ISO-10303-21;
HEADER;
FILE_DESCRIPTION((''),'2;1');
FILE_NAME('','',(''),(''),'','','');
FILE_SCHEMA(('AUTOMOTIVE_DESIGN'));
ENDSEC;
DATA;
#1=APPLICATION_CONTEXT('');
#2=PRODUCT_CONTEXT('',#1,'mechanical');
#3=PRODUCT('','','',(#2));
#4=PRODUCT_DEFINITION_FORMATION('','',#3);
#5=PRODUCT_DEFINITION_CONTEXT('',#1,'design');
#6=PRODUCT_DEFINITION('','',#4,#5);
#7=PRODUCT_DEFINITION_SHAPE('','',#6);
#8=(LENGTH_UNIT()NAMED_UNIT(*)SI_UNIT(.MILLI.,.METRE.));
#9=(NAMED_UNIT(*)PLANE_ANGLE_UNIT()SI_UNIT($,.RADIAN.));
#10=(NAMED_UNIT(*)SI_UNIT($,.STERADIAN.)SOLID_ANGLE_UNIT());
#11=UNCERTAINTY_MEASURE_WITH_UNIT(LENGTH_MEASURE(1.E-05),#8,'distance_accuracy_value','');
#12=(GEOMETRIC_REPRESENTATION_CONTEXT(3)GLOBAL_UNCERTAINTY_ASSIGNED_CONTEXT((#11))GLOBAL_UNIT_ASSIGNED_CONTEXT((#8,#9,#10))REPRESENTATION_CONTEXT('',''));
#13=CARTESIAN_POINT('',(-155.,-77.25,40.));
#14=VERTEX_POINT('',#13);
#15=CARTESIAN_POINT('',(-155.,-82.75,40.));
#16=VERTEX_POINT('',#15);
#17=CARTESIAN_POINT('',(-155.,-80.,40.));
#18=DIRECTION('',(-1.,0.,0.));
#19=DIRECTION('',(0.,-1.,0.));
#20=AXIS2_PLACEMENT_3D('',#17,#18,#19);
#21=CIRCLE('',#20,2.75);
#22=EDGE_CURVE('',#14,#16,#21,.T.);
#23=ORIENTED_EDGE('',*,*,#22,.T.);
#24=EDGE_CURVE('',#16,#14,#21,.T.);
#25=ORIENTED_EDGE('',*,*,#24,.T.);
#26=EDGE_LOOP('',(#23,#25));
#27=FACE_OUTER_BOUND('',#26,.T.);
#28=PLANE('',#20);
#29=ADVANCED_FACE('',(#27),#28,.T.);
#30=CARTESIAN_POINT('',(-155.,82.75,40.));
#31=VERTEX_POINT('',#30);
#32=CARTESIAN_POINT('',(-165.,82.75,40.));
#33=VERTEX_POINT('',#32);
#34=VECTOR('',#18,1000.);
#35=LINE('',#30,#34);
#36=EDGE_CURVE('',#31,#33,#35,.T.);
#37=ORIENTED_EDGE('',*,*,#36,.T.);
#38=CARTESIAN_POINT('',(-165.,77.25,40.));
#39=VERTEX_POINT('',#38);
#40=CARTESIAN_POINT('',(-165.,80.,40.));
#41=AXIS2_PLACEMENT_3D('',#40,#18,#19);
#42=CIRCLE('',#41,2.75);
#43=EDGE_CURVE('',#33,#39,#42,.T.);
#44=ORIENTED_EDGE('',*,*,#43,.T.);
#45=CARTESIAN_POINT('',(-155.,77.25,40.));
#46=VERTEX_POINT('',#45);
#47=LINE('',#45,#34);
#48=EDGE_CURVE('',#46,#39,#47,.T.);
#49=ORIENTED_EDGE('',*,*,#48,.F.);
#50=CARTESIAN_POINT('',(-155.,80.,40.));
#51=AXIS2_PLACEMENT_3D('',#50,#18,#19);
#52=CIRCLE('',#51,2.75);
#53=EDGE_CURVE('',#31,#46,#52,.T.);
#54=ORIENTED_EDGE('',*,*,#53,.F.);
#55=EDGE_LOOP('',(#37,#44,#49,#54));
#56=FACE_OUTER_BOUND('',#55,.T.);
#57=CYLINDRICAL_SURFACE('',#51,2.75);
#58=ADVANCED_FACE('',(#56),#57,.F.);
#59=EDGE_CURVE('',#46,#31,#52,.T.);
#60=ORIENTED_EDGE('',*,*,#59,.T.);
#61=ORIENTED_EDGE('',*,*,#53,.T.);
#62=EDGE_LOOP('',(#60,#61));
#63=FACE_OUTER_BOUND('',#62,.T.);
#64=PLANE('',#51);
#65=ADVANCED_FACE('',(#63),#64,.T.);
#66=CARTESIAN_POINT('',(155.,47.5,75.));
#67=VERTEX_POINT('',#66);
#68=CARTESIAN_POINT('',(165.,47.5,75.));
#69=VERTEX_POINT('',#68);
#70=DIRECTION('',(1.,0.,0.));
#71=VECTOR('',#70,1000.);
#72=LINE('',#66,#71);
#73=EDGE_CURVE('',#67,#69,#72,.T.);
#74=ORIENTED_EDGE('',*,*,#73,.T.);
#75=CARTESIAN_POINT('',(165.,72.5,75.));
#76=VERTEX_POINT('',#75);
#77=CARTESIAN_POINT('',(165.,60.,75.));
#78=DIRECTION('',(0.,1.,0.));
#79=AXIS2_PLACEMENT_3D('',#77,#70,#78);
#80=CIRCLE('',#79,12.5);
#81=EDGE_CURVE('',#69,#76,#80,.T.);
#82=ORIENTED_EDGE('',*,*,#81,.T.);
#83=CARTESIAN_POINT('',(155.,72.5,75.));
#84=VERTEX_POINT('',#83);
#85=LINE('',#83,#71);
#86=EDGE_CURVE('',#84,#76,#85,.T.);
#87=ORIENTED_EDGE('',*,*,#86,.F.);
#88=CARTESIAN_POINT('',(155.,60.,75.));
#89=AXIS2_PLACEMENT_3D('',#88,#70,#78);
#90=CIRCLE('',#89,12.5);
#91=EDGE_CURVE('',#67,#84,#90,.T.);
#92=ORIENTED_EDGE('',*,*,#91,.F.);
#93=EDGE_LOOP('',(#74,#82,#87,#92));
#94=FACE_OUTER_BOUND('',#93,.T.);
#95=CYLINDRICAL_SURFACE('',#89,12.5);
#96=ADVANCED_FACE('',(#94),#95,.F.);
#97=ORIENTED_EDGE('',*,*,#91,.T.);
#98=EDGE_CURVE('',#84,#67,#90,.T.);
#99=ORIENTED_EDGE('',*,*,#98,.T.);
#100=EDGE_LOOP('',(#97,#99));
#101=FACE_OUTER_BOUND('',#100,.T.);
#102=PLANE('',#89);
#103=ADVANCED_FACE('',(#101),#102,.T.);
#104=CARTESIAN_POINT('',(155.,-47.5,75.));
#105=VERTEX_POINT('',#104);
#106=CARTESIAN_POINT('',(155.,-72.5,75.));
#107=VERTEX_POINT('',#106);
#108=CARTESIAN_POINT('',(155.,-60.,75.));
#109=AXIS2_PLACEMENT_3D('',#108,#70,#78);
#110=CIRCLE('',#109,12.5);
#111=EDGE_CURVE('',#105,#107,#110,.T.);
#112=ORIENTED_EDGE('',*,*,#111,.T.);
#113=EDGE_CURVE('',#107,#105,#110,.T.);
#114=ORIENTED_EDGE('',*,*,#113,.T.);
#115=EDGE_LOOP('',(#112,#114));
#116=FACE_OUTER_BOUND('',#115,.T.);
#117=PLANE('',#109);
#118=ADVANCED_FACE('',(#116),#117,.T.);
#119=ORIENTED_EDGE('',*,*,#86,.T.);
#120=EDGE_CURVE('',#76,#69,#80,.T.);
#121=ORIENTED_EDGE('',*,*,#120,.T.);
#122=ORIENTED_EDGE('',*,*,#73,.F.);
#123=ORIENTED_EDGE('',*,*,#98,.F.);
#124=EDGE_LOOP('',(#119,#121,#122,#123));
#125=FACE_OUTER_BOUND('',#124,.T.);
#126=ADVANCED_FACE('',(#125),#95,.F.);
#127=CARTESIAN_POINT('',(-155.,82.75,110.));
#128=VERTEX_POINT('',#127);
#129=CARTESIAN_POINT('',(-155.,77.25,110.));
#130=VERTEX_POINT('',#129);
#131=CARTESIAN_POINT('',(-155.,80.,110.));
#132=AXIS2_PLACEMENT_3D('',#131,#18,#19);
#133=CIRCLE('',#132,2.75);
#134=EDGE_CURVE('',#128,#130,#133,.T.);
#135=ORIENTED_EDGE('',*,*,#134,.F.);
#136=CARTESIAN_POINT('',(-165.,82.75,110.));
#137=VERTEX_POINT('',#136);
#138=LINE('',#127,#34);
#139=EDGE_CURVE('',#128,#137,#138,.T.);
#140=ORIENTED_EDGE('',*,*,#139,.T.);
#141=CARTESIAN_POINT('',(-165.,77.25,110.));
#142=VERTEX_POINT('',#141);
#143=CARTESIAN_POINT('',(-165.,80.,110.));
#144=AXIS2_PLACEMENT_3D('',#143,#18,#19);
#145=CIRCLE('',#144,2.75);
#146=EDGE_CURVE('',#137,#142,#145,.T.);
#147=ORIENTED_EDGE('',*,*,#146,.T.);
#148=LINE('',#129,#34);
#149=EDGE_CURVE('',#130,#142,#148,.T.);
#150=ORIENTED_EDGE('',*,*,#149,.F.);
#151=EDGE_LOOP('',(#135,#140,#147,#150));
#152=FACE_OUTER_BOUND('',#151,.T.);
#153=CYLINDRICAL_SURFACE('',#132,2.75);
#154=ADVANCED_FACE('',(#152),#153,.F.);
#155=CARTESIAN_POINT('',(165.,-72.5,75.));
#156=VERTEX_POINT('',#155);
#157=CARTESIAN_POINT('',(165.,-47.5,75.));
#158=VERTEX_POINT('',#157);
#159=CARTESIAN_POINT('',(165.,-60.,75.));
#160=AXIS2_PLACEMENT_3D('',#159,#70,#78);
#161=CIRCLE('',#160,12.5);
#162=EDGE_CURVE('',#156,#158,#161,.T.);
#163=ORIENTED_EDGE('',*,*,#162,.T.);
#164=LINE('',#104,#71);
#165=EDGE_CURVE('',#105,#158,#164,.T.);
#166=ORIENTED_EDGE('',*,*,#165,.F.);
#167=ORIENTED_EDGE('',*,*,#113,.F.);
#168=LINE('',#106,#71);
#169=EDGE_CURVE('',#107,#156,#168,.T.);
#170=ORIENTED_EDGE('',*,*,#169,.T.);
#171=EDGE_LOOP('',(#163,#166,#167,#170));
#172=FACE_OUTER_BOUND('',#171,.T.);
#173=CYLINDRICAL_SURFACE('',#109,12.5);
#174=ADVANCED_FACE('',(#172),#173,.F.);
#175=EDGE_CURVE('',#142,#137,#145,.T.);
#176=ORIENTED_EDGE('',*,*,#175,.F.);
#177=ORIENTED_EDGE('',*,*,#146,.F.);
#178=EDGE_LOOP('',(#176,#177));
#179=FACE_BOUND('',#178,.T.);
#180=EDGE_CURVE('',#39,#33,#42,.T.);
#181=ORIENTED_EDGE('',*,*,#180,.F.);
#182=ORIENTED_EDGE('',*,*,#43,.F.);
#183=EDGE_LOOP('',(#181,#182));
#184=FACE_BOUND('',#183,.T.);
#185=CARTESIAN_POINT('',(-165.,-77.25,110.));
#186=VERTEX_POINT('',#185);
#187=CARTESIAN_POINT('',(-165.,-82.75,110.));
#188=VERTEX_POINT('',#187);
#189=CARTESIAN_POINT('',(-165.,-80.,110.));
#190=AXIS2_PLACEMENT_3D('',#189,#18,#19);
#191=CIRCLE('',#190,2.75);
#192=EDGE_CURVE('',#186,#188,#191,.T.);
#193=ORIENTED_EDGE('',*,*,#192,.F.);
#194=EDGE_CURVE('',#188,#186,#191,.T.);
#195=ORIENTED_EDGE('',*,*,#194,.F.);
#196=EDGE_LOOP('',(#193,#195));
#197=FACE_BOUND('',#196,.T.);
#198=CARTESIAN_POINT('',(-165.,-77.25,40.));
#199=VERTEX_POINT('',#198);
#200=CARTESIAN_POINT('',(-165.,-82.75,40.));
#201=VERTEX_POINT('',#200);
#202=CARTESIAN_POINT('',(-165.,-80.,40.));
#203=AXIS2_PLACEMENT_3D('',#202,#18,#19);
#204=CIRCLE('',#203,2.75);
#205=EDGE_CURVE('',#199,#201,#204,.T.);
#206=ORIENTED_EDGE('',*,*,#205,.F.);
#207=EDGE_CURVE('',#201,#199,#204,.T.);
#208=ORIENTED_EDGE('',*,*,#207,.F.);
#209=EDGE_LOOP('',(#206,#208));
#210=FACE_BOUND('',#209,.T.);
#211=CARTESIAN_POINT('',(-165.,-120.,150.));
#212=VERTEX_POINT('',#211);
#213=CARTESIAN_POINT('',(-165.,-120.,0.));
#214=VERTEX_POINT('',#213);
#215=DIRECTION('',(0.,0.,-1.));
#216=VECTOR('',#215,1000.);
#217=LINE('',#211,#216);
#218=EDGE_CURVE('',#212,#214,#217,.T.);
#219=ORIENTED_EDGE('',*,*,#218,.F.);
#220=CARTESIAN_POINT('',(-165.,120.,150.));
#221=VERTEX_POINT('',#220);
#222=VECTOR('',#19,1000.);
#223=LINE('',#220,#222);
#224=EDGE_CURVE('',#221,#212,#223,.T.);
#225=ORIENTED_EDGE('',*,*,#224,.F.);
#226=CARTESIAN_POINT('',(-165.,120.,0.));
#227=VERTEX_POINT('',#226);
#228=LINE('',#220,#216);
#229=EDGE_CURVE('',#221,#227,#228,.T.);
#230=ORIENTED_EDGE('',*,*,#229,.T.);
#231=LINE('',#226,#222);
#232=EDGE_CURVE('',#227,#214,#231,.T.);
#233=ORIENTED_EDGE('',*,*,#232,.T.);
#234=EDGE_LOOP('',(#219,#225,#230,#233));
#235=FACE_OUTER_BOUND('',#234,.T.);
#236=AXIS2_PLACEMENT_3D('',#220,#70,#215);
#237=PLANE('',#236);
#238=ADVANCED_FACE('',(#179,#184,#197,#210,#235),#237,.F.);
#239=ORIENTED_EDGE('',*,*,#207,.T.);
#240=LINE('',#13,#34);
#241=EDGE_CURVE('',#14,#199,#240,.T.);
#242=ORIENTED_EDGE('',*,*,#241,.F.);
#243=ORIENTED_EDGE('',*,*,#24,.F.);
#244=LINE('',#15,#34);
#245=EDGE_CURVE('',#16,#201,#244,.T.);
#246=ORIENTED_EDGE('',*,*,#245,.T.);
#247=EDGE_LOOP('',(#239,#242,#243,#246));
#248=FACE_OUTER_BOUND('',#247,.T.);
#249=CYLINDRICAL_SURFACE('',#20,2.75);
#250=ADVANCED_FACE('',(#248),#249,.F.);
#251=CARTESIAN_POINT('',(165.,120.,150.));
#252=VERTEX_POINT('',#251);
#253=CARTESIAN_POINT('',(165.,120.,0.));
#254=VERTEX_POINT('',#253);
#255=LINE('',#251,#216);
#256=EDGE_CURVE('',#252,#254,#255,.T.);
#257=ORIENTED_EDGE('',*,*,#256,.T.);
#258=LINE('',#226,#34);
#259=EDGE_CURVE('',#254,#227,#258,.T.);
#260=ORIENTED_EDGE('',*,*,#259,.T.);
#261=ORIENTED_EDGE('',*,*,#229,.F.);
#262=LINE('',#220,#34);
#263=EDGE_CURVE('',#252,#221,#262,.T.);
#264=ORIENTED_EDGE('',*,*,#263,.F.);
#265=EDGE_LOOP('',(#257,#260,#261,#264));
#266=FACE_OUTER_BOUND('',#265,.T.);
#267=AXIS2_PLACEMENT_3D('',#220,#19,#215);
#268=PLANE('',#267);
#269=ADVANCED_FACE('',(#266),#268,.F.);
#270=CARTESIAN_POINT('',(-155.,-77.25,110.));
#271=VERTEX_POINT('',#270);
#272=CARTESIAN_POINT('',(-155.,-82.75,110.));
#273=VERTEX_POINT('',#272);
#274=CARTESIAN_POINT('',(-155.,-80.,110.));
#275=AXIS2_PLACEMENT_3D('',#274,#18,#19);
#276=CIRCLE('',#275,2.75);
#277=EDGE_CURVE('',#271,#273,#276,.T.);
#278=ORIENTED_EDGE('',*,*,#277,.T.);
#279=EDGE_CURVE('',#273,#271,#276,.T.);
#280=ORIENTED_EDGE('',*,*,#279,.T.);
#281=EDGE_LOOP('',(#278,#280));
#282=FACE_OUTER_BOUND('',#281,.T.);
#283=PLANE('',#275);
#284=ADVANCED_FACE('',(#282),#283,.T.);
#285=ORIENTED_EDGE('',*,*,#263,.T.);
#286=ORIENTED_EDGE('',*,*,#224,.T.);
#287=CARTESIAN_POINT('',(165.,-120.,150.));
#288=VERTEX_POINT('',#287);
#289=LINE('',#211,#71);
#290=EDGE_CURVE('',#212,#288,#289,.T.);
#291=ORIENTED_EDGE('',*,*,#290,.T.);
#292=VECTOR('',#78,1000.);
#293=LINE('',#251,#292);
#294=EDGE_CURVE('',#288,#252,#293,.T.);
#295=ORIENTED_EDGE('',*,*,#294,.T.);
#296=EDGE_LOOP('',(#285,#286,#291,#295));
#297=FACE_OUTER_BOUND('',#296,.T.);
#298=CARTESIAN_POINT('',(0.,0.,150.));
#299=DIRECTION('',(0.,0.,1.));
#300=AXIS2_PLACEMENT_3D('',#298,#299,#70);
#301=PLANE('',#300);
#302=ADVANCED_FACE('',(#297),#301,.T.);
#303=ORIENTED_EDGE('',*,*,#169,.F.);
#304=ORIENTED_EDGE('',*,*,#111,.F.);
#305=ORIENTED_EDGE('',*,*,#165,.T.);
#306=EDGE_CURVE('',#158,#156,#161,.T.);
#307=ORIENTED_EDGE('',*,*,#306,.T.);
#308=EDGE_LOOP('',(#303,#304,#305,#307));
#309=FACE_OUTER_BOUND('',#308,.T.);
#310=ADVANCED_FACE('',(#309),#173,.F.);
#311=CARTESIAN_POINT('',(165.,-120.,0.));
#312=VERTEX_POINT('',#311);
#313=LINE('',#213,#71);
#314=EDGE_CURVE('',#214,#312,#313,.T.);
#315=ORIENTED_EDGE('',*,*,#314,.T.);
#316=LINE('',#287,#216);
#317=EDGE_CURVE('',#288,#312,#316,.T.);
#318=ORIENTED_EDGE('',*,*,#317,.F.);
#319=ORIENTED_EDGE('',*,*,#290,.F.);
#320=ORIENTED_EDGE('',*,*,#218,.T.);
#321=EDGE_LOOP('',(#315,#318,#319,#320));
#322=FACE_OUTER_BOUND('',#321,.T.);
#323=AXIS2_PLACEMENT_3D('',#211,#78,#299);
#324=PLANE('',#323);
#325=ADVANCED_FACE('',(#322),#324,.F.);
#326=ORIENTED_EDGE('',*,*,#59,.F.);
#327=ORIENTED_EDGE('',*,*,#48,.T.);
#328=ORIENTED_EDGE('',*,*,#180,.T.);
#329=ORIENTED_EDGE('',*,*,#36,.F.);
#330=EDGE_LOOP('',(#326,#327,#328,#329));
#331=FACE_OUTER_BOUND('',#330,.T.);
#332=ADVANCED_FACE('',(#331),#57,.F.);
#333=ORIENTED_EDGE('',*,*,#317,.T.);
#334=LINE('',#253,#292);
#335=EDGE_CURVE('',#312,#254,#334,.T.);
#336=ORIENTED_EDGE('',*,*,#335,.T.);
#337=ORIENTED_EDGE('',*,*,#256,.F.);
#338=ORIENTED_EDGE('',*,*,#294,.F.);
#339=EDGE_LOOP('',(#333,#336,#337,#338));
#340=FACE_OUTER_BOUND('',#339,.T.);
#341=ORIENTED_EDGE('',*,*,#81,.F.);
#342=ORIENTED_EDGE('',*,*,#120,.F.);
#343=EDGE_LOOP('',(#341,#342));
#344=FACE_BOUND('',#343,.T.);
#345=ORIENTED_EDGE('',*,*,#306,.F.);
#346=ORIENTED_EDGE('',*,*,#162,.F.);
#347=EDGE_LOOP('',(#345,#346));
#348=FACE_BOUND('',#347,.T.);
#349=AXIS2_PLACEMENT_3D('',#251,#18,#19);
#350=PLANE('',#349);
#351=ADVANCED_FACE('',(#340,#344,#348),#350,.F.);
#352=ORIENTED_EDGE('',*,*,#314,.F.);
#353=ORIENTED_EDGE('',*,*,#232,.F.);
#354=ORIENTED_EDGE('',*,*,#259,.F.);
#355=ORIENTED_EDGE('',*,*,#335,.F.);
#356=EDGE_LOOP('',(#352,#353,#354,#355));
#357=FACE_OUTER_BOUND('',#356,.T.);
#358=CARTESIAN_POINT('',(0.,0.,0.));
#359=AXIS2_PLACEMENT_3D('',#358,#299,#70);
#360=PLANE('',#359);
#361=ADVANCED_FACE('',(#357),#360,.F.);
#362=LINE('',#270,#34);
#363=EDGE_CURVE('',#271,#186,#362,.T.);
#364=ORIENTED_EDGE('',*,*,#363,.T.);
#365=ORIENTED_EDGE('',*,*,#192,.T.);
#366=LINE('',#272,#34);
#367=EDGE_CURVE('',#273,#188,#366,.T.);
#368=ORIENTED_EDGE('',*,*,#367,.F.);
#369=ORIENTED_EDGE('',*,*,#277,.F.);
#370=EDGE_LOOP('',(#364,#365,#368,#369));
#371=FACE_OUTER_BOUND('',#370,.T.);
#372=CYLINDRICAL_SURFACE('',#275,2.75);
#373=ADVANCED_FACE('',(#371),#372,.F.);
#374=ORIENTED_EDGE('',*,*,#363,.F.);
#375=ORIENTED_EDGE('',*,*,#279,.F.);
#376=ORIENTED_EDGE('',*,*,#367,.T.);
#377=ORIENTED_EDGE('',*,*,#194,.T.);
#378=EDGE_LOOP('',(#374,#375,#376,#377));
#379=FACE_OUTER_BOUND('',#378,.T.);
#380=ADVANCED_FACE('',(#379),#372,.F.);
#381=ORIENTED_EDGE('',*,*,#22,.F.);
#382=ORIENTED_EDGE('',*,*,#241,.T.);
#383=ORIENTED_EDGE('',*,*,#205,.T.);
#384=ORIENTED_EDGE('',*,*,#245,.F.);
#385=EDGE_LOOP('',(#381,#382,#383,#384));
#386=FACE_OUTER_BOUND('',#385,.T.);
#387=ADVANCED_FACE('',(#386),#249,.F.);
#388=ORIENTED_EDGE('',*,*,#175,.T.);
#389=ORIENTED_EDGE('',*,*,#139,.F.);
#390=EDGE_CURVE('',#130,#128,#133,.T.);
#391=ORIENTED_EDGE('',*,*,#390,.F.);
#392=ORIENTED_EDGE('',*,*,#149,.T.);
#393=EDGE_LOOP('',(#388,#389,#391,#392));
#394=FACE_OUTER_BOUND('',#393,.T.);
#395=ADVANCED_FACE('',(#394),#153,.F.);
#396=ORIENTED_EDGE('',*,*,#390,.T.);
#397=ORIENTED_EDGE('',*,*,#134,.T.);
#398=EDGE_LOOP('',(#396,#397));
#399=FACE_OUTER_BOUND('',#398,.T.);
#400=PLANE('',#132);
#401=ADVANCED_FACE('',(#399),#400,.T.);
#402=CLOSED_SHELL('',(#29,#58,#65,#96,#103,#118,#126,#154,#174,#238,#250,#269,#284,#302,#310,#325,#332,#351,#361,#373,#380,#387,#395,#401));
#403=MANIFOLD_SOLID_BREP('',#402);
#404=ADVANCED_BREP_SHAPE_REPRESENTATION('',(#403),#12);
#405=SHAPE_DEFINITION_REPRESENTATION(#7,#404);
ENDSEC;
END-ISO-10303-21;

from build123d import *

# Parameters (mm, degrees)
SKETCH_1_W          = 330
SKETCH_1_H          = 240
EXTRUDE_1_DEPTH     = 150
SKETCH_2_R          = 12.5
CUT_EXTRUDE_1_DEPTH = 10
SKETCH_3_R          = 2.75
CUT_EXTRUDE_2_DEPTH = 10


with BuildPart() as part:
    # 草图1 → 凸台-拉伸1 (new body)
    with BuildSketch(Plane.XY):
        Rectangle(SKETCH_1_W, SKETCH_1_H)
    extrude(amount=EXTRUDE_1_DEPTH)

    # 草图2 → 切除-拉伸1 (cut)
    with BuildSketch(Plane(origin=(165, 0, 0), x_dir=(0, 0, -1), z_dir=(1, 0, 0))):
        with Locations(Location((-75, 60, 0), (0, 0, 90))):
            Circle(SKETCH_2_R)
        with Locations(Location((-75, -60, 0), (0, 0, 90))):
            Circle(SKETCH_2_R)
    extrude(amount=-CUT_EXTRUDE_1_DEPTH, mode=Mode.SUBTRACT)

    # 草图3 → 切除-拉伸2 (cut)
    with BuildSketch(Plane.ZY.offset(165)):
        with Locations(Location((40, 80, 0), (0, 0, 270))):
            Circle(SKETCH_3_R)
        with Locations(Location((110, 80, 0), (0, 0, 270))):
            Circle(SKETCH_3_R)
        with Locations(Location((110, -80, 0), (0, 0, 270))):
            Circle(SKETCH_3_R)
        with Locations(Location((40, -80, 0), (0, 0, 270))):
            Circle(SKETCH_3_R)
    extrude(amount=-CUT_EXTRUDE_2_DEPTH, mode=Mode.SUBTRACT)


solid = part.part
